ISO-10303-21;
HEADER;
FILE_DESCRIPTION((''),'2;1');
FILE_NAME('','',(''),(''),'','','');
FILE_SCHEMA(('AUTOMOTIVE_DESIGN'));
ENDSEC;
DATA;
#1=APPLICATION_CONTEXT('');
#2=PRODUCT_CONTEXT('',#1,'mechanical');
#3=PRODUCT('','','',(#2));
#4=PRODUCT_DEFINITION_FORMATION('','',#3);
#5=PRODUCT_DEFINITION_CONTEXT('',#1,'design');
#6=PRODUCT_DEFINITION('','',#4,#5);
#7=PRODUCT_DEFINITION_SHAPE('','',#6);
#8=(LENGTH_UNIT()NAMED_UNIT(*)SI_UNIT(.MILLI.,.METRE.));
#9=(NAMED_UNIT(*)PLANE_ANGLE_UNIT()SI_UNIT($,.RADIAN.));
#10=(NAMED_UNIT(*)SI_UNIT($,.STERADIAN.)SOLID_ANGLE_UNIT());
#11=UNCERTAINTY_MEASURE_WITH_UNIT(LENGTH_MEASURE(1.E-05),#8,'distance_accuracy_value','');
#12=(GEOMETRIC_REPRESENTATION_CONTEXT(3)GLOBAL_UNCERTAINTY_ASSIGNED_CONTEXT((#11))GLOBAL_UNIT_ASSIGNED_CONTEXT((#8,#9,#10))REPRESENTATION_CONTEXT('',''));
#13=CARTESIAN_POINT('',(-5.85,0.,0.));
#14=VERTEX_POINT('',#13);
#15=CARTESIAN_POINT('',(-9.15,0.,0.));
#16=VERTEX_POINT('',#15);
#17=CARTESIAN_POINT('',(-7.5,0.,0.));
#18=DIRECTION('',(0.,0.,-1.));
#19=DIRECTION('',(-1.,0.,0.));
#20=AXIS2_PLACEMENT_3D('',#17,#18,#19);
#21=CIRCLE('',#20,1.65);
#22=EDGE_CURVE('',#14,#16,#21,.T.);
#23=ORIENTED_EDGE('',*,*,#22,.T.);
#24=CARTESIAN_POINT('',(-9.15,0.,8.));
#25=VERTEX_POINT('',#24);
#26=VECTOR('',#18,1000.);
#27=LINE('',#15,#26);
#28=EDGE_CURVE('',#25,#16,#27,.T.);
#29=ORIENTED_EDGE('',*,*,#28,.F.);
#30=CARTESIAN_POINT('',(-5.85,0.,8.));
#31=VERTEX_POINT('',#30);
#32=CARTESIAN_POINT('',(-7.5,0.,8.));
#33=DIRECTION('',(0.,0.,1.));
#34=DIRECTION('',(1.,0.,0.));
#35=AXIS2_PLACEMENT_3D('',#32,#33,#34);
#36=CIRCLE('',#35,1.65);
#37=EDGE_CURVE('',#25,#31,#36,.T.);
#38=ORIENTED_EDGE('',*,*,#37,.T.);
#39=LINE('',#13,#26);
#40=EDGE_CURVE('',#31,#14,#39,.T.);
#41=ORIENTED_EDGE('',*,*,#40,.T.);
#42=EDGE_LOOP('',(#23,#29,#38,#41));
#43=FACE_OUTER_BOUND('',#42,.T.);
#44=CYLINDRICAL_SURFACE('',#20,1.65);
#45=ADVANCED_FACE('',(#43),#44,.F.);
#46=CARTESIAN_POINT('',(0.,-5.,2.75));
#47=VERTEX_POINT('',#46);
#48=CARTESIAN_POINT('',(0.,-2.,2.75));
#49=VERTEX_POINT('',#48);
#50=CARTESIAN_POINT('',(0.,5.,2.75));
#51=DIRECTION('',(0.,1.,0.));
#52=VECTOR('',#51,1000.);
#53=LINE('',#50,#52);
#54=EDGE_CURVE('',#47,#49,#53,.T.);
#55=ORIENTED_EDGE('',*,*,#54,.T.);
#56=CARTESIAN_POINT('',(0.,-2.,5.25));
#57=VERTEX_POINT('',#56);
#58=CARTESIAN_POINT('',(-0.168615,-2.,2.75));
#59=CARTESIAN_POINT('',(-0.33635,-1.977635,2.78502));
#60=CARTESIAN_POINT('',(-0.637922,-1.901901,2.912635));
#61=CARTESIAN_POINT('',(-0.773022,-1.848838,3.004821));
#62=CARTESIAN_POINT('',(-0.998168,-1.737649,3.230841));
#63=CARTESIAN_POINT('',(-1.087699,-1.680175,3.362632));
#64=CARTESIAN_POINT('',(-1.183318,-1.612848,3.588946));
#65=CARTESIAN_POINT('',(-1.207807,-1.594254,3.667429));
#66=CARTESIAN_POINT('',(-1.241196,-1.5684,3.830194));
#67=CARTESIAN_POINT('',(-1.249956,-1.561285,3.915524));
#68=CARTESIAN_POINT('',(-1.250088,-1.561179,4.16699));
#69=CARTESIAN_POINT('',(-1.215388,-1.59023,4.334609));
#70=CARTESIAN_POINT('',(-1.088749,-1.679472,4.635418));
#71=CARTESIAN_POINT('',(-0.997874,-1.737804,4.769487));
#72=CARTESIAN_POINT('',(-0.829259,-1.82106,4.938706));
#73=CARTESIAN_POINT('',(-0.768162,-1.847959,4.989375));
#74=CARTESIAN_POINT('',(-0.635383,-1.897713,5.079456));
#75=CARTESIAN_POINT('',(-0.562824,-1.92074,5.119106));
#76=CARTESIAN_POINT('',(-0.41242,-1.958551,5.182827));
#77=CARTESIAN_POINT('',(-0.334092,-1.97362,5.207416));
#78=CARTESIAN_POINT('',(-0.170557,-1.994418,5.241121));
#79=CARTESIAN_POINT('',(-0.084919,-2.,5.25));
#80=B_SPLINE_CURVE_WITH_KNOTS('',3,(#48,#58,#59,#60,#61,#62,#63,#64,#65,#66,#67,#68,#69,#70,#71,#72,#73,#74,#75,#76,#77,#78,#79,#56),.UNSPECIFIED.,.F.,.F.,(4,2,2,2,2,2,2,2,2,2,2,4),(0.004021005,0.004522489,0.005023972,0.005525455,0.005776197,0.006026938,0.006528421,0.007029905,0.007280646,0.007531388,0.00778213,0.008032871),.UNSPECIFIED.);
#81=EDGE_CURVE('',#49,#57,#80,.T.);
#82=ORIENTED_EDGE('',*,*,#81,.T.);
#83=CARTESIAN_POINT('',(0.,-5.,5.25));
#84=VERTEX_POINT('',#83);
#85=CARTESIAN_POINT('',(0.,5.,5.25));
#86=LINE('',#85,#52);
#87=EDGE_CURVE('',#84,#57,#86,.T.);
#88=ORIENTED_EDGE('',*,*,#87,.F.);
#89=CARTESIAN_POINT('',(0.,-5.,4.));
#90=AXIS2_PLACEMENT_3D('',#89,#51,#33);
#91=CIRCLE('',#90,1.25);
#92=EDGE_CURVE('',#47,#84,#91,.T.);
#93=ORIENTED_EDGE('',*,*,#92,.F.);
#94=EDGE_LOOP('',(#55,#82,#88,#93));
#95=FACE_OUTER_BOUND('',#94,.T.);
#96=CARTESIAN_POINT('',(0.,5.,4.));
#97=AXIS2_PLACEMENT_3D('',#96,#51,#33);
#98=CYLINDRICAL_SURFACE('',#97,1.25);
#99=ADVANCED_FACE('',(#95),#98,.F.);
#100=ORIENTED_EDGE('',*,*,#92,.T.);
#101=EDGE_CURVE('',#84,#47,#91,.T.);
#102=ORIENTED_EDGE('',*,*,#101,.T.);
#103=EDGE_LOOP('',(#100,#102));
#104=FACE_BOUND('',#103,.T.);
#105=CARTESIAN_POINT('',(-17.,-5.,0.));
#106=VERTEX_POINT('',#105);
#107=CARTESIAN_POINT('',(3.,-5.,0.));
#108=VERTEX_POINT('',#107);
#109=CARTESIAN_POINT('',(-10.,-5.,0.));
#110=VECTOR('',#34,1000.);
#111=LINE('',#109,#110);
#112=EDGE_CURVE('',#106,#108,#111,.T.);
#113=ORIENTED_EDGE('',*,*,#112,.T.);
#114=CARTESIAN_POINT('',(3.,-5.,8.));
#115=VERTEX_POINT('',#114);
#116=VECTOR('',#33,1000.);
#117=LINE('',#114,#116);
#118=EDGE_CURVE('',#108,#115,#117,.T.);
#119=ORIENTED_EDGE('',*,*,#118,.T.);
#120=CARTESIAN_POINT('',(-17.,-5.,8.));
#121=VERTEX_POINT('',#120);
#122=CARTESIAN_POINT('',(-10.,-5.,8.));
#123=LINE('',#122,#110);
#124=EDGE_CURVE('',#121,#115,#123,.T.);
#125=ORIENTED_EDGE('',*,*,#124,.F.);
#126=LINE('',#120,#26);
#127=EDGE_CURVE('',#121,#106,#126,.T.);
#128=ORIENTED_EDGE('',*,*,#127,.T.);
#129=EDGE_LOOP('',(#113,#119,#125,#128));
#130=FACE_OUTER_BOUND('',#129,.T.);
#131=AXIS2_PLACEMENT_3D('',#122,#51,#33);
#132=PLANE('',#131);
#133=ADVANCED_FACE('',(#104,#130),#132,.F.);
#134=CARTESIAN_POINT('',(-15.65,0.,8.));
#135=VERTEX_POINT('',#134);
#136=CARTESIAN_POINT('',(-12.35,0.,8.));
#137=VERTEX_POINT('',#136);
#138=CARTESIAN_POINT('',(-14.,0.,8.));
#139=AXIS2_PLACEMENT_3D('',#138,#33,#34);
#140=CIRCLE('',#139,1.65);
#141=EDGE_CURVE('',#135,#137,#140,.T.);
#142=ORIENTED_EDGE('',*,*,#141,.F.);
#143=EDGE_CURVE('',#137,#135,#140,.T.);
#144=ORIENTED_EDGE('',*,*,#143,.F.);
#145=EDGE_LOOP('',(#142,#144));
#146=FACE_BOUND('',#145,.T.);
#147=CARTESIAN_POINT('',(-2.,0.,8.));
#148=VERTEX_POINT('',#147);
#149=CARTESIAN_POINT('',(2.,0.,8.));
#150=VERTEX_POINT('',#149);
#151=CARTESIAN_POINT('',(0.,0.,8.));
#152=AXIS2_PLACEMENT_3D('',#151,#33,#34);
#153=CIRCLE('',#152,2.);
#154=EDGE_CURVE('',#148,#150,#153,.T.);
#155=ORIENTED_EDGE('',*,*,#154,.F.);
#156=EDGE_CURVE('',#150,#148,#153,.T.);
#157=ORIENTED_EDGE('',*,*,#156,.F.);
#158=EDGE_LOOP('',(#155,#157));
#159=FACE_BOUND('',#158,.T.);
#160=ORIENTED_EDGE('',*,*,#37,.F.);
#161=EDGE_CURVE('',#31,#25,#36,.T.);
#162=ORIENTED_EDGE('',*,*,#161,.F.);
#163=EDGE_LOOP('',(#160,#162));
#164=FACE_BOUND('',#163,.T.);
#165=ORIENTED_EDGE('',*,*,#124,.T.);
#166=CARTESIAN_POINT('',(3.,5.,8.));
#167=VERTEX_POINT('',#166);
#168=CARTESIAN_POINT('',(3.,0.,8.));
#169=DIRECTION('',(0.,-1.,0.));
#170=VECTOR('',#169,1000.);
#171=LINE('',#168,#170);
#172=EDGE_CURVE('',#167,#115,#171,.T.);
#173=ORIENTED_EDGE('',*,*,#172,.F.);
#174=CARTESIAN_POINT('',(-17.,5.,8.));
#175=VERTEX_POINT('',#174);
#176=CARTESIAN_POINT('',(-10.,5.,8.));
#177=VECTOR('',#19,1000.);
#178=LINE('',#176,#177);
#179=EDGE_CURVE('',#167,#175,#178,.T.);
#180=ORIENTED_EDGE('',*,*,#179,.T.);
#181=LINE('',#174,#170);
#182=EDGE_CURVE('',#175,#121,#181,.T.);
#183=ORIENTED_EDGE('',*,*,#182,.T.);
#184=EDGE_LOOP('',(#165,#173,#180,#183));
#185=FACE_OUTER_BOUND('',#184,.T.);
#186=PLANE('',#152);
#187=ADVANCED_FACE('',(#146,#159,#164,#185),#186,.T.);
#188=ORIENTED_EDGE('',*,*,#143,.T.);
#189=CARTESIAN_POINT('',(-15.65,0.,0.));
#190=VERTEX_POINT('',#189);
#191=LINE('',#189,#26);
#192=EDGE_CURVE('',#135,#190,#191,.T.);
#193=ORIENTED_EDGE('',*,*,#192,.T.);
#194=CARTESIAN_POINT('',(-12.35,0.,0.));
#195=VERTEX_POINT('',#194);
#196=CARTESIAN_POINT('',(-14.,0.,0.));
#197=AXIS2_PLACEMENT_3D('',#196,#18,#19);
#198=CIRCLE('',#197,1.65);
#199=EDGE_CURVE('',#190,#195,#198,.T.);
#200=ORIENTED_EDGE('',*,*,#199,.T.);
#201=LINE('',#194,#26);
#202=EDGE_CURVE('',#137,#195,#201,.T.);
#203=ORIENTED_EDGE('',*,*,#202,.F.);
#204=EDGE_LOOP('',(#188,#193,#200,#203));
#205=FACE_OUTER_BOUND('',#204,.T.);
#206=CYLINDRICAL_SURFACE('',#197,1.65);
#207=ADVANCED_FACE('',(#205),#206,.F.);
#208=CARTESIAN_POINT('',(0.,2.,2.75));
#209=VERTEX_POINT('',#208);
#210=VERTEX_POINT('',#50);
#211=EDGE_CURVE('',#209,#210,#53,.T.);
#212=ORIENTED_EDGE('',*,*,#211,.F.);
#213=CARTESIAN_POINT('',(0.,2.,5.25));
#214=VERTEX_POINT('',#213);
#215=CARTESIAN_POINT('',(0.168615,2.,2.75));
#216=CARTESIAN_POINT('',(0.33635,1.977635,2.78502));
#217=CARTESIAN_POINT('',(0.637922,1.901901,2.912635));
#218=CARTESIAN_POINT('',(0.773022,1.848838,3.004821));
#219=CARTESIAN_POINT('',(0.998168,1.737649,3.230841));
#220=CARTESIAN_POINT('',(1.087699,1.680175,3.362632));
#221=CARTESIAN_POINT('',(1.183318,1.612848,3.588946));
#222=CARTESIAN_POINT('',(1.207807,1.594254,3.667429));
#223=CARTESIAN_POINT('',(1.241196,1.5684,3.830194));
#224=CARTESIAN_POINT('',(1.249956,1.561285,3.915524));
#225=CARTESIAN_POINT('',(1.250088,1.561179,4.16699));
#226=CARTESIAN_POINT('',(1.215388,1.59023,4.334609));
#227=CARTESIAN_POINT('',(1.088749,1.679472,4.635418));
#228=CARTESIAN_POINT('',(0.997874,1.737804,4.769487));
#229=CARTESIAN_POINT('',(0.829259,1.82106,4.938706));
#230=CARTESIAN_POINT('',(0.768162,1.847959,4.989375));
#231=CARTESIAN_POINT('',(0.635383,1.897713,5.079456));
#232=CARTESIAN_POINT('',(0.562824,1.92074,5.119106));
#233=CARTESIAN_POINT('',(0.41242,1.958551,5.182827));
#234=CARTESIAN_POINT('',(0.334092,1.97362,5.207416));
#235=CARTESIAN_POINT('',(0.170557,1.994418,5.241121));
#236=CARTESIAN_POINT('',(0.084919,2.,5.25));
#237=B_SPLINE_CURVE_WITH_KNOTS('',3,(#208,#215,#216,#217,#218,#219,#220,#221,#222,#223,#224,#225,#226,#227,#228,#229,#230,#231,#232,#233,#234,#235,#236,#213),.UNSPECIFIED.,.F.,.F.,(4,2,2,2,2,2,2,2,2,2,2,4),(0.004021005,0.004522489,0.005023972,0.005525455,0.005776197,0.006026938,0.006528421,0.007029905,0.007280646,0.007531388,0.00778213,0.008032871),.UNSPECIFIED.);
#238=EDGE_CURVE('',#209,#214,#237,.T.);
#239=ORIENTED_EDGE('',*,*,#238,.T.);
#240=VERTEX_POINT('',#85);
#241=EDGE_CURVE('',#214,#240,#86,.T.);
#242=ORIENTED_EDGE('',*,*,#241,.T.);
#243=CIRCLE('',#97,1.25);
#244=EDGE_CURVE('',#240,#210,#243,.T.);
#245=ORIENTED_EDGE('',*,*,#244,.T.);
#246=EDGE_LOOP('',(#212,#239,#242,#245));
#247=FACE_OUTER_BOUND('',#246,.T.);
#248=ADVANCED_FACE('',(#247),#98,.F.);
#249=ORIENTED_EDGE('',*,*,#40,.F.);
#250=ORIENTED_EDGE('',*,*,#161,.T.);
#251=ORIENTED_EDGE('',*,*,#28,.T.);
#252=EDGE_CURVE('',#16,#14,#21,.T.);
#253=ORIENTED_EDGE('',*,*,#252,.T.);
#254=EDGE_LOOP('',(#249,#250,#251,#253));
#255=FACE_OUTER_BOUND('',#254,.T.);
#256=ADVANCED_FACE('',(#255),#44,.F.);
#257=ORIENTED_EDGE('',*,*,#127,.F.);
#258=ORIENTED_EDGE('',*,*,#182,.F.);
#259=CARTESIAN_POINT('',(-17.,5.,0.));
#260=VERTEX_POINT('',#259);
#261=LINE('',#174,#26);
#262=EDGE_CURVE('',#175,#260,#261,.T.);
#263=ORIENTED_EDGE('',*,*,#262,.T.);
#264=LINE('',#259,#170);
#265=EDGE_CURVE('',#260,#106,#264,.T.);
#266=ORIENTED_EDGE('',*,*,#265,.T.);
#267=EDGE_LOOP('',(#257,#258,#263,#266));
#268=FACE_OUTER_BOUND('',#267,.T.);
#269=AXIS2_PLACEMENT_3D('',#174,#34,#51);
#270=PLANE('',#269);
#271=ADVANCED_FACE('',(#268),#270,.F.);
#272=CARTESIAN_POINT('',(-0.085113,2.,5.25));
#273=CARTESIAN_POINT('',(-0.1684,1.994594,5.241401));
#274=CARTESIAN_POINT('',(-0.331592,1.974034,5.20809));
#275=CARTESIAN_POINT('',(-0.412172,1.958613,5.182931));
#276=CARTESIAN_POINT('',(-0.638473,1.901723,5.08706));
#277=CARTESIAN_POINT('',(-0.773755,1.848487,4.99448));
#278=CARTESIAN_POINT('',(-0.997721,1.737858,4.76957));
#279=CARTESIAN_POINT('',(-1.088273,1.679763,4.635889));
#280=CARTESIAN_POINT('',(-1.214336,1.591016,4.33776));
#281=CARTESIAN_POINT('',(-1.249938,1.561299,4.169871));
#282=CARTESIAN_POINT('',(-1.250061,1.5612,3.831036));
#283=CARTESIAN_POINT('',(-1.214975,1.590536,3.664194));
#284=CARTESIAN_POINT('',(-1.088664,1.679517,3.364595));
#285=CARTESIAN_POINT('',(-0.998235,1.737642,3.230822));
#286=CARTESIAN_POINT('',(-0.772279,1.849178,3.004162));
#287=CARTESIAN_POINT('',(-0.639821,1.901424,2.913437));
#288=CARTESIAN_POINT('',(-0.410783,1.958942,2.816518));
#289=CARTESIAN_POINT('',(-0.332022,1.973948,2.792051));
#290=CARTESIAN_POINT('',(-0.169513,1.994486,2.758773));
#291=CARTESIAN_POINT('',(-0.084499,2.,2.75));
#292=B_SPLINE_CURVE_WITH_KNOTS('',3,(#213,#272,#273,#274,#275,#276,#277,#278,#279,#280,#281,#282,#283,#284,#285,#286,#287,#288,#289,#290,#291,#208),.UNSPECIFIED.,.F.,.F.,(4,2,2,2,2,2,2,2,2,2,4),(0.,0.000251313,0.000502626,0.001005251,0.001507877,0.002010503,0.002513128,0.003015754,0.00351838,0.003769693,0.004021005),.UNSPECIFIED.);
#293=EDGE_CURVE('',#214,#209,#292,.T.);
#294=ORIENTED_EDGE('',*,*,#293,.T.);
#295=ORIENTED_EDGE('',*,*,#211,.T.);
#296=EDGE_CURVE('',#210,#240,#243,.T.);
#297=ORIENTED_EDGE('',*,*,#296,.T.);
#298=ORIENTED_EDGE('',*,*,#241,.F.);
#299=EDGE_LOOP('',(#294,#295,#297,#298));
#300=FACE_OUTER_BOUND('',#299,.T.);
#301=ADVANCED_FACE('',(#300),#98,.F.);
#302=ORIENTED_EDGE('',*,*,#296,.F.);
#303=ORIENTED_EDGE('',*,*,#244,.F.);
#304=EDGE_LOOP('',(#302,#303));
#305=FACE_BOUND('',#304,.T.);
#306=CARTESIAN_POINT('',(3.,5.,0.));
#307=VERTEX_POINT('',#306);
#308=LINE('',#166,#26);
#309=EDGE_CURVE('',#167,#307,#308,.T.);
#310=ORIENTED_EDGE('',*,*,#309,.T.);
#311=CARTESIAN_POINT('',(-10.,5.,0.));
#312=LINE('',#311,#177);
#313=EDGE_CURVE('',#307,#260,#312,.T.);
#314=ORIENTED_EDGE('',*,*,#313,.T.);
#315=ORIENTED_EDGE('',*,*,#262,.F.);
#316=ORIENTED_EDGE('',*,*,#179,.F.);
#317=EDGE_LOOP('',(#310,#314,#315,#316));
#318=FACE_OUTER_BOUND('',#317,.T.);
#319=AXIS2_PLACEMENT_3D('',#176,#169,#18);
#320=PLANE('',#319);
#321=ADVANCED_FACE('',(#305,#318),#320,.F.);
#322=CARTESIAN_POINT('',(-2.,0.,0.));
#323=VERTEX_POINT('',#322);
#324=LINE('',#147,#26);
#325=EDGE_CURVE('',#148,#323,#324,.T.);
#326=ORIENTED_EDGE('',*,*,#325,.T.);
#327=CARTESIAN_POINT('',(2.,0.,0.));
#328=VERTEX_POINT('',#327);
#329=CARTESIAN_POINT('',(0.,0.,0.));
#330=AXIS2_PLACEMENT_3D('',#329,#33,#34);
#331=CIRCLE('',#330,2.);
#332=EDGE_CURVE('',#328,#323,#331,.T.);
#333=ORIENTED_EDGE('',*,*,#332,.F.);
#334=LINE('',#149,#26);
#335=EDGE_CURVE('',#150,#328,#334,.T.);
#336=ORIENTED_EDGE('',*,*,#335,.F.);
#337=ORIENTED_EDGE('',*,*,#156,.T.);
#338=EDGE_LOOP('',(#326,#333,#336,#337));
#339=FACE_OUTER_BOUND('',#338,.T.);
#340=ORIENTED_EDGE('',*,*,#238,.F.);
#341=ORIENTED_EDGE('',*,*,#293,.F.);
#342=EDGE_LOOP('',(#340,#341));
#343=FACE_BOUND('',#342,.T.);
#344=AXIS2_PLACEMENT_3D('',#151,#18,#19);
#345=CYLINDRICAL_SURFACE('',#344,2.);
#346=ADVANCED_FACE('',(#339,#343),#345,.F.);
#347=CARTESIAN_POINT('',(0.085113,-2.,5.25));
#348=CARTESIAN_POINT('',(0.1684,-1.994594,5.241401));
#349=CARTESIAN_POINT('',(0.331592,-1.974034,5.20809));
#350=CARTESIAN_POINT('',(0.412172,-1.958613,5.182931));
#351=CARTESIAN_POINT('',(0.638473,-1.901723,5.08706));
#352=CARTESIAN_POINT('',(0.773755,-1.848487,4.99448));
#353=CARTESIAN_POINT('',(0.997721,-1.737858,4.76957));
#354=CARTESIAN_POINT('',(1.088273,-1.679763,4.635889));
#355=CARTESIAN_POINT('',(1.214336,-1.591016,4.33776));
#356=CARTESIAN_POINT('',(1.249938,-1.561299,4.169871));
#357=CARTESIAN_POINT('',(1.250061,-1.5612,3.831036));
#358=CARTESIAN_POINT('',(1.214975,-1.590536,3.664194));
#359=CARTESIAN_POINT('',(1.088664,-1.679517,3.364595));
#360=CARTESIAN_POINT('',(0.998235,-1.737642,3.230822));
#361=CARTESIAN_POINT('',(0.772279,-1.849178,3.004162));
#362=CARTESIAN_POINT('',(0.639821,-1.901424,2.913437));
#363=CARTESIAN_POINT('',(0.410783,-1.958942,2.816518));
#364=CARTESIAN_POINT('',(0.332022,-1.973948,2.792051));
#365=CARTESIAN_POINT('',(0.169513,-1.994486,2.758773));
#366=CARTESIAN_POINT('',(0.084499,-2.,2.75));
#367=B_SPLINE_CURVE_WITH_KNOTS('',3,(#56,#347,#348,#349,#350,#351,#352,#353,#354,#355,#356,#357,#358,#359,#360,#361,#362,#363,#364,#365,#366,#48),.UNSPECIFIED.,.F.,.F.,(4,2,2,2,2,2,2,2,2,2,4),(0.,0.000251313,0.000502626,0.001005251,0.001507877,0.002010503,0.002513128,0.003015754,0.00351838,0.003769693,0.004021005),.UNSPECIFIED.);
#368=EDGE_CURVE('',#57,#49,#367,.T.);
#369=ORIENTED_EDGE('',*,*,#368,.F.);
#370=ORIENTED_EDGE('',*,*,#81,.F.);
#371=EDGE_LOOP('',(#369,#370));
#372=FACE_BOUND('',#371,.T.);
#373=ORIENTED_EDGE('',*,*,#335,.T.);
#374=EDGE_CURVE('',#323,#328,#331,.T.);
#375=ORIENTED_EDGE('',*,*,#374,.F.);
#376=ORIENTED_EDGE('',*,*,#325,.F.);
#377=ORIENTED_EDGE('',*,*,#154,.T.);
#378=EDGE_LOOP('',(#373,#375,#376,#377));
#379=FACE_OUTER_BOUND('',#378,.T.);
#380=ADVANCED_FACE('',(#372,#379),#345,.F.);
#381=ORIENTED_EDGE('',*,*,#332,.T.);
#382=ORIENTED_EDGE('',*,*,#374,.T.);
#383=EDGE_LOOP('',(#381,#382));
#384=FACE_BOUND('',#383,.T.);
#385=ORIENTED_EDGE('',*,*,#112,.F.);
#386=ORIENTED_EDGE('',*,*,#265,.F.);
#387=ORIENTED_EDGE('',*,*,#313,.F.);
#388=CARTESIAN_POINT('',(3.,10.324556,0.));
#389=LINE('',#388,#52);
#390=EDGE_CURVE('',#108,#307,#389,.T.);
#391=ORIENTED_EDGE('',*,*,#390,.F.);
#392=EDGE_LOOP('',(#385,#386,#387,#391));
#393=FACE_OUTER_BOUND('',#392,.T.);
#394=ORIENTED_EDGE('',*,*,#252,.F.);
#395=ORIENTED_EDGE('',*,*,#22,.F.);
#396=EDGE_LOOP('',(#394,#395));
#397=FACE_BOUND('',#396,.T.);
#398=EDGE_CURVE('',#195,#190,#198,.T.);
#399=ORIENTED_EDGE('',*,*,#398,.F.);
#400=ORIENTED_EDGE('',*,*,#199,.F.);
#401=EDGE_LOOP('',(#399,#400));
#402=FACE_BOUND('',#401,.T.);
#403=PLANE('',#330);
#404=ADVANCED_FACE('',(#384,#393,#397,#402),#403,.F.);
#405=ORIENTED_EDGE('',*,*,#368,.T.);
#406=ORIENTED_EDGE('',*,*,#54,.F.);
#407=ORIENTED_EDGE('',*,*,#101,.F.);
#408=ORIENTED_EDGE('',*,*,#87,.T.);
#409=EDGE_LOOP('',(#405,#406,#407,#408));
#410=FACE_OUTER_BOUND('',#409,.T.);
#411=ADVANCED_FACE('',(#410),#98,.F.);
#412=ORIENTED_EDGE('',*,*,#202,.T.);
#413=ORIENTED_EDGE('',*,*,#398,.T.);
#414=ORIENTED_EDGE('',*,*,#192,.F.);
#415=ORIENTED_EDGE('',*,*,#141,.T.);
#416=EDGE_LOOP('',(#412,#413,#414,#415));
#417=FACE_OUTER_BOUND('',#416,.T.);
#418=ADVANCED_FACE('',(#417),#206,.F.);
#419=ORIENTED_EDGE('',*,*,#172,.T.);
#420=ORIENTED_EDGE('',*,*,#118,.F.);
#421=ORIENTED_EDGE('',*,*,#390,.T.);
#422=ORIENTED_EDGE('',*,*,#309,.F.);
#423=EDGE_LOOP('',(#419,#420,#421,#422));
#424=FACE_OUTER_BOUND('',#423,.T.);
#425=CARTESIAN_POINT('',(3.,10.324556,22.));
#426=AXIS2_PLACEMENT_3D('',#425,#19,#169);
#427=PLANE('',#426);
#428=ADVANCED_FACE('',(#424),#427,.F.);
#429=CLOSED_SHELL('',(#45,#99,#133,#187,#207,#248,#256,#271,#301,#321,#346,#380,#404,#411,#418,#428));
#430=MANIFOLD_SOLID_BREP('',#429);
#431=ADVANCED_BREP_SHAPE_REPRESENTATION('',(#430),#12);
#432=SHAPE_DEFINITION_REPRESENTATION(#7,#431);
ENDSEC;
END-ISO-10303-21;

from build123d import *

# Parameters (mm, degrees)
SKETCH_1_W                  = 20
SKETCH_1_H                  = 10
SKETCH_1_R                  = 2
EXTRUDE_1_DEPTH             = 8
SKETCH_2_W                  = 9.758246521
SKETCH_2_H                  = 16.171909484
CUT_EXTRUDE_1_DEPTH         = 22
MOVE_FACE_1_BY              = 7
HOLE_WIZARD_3_3_3_3_1_D     = 3.3
HOLE_WIZARD_3_3_3_3_1_DEPTH = 11.5
HOLE_WIZARD_3_3_3_3_1_TIP   = 0.991420021
HOLE_WIZARD_M3_1_D          = 2.5


with BuildPart() as part:
    # 草图1 → 凸台-拉伸1 (new body)
    with BuildSketch(Plane.XY):
        Rectangle(SKETCH_1_W, SKETCH_1_H)
        Circle(SKETCH_1_R, mode=Mode.SUBTRACT)
    extrude(amount=EXTRUDE_1_DEPTH)

    # 草图2 → 切除-拉伸1 (cut)
    with BuildSketch(Plane(origin=(0, 0, 0), x_dir=(-1, 0, 0), z_dir=(0, 0, -1))):
        with Locations((-7.879123261, 2.238600796)):
            Rectangle(SKETCH_2_W, SKETCH_2_H)
    extrude(amount=-CUT_EXTRUDE_1_DEPTH, mode=Mode.SUBTRACT)

    # Move Face 1: a face moved outward by 7.0
    extrude(part.faces().sort_by_distance((-10, 0, 4))[0], amount=MOVE_FACE_1_BY, dir=(-1, 0, 0))

    # Ø3.3 (3.3) 直径孔1
    with Locations(Plane(origin=(0, 0, 0), x_dir=(-1, 0, 0), z_dir=(0, 0, -1))):
        with Locations((7.5, 0), (14, 0)):
            Hole(HOLE_WIZARD_3_3_3_3_1_D / 2, depth=HOLE_WIZARD_3_3_3_3_1_DEPTH)
            with Locations((0, 0, -(HOLE_WIZARD_3_3_3_3_1_DEPTH + HOLE_WIZARD_3_3_3_3_1_TIP / 2))):  # 118° drill point
                Cone(0, HOLE_WIZARD_3_3_3_3_1_D / 2, HOLE_WIZARD_3_3_3_3_1_TIP, mode=Mode.SUBTRACT)

    # M3 螺纹孔1 (through all)
    with Locations(Plane(origin=(0, 5, 0), x_dir=(1, 0, 0), z_dir=(0, 1, 0))):
        with Locations((0, -4)):
            Hole(HOLE_WIZARD_M3_1_D / 2)


solid = part.part
